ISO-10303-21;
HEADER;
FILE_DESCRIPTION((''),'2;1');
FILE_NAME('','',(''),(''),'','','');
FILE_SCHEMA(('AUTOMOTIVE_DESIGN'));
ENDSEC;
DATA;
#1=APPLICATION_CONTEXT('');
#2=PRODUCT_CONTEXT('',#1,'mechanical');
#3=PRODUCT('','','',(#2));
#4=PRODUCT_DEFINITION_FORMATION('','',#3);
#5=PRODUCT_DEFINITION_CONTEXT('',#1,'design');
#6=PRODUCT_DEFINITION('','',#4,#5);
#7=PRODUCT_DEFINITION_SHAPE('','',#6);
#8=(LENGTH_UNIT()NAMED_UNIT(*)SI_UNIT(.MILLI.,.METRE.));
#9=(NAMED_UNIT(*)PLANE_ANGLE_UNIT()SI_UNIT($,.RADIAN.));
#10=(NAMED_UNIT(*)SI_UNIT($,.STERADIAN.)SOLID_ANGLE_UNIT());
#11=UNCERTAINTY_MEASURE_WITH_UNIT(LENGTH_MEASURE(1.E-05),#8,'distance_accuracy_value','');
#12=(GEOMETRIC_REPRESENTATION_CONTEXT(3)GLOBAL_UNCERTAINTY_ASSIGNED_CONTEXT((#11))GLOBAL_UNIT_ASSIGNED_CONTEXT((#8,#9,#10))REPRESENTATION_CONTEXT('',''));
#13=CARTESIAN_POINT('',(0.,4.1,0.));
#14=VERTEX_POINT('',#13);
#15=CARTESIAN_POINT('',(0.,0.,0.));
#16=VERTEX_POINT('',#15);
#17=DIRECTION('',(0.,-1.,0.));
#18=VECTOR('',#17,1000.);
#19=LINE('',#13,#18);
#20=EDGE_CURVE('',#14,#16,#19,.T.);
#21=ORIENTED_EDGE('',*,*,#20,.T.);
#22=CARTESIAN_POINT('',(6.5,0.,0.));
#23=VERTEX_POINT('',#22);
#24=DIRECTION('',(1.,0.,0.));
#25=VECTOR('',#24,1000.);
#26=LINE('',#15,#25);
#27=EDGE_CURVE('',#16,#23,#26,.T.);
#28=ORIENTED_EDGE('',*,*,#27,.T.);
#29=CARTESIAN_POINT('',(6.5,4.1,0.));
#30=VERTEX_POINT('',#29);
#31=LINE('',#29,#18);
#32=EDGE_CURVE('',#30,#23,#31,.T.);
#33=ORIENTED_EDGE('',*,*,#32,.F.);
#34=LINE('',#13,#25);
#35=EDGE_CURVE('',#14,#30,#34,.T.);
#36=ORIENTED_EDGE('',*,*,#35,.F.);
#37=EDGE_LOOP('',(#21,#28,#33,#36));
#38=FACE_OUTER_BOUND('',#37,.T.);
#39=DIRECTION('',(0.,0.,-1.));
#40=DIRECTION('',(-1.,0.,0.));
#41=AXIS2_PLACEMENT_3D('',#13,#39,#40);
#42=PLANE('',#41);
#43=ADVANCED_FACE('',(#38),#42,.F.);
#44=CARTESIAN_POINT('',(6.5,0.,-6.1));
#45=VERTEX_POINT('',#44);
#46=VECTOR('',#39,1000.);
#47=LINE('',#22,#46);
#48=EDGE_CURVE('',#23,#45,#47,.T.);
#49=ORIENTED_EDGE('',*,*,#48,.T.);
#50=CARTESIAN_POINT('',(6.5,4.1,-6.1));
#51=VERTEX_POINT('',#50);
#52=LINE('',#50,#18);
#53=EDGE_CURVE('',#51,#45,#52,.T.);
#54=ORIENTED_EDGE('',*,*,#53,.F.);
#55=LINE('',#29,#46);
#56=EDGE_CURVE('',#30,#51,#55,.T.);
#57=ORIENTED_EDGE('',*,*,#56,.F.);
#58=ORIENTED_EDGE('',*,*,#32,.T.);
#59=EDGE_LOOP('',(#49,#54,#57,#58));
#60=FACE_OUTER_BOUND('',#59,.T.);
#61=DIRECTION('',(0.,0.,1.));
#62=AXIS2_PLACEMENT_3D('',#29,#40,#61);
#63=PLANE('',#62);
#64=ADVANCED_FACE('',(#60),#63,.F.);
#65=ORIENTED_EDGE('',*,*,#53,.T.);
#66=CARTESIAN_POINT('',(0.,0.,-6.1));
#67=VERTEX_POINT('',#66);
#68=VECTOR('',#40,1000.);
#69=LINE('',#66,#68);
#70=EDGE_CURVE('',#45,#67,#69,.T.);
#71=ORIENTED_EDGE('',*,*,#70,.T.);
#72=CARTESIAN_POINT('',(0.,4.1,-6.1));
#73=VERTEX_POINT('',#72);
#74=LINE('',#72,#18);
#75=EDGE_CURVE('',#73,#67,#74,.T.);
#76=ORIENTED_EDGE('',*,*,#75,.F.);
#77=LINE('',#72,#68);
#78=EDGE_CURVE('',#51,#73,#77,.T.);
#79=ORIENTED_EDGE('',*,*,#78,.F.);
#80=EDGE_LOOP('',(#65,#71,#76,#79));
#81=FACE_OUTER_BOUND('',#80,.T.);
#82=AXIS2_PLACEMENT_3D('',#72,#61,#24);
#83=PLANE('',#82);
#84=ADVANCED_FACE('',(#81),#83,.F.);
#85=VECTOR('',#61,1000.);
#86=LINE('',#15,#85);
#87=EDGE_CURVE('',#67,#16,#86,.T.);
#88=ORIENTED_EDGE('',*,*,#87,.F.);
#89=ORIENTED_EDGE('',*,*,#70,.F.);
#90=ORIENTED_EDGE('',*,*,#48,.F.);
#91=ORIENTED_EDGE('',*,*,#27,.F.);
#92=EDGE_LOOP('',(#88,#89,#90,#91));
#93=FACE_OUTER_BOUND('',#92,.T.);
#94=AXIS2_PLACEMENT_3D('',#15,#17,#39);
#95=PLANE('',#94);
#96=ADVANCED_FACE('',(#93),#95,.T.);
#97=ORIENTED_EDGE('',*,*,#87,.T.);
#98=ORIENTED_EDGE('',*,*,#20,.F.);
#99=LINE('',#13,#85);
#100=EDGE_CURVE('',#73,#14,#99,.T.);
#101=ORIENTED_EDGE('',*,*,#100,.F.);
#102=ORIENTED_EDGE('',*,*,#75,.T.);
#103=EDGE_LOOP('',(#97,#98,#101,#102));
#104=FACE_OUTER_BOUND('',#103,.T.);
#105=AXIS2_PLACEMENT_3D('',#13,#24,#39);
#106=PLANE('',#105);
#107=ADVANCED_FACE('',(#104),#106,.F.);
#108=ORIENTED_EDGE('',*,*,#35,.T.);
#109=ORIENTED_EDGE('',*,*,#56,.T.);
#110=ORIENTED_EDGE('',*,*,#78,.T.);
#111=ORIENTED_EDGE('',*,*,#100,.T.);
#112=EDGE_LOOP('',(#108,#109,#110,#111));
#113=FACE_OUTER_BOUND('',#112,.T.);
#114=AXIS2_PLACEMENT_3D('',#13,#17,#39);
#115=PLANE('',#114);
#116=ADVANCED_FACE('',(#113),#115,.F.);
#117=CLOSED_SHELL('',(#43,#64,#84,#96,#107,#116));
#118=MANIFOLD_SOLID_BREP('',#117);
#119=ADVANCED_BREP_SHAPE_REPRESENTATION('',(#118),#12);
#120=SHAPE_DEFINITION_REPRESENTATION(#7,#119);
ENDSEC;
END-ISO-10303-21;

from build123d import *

# Parameters (mm, degrees)
SKETCH1_W           = 6.5
SKETCH1_H           = 6.1
BOSS_EXTRUDE1_DEPTH = 4.1


with BuildPart() as part:
    # Sketch1 → Boss-Extrude1 (new body)
    with BuildSketch(Plane(origin=(0, 0, 0), x_dir=(1, 0, 0), z_dir=(0, 1, 0))):
        with Locations((3.25, 3.05)):
            Rectangle(SKETCH1_W, SKETCH1_H)
    extrude(amount=BOSS_EXTRUDE1_DEPTH)


solid = part.part
